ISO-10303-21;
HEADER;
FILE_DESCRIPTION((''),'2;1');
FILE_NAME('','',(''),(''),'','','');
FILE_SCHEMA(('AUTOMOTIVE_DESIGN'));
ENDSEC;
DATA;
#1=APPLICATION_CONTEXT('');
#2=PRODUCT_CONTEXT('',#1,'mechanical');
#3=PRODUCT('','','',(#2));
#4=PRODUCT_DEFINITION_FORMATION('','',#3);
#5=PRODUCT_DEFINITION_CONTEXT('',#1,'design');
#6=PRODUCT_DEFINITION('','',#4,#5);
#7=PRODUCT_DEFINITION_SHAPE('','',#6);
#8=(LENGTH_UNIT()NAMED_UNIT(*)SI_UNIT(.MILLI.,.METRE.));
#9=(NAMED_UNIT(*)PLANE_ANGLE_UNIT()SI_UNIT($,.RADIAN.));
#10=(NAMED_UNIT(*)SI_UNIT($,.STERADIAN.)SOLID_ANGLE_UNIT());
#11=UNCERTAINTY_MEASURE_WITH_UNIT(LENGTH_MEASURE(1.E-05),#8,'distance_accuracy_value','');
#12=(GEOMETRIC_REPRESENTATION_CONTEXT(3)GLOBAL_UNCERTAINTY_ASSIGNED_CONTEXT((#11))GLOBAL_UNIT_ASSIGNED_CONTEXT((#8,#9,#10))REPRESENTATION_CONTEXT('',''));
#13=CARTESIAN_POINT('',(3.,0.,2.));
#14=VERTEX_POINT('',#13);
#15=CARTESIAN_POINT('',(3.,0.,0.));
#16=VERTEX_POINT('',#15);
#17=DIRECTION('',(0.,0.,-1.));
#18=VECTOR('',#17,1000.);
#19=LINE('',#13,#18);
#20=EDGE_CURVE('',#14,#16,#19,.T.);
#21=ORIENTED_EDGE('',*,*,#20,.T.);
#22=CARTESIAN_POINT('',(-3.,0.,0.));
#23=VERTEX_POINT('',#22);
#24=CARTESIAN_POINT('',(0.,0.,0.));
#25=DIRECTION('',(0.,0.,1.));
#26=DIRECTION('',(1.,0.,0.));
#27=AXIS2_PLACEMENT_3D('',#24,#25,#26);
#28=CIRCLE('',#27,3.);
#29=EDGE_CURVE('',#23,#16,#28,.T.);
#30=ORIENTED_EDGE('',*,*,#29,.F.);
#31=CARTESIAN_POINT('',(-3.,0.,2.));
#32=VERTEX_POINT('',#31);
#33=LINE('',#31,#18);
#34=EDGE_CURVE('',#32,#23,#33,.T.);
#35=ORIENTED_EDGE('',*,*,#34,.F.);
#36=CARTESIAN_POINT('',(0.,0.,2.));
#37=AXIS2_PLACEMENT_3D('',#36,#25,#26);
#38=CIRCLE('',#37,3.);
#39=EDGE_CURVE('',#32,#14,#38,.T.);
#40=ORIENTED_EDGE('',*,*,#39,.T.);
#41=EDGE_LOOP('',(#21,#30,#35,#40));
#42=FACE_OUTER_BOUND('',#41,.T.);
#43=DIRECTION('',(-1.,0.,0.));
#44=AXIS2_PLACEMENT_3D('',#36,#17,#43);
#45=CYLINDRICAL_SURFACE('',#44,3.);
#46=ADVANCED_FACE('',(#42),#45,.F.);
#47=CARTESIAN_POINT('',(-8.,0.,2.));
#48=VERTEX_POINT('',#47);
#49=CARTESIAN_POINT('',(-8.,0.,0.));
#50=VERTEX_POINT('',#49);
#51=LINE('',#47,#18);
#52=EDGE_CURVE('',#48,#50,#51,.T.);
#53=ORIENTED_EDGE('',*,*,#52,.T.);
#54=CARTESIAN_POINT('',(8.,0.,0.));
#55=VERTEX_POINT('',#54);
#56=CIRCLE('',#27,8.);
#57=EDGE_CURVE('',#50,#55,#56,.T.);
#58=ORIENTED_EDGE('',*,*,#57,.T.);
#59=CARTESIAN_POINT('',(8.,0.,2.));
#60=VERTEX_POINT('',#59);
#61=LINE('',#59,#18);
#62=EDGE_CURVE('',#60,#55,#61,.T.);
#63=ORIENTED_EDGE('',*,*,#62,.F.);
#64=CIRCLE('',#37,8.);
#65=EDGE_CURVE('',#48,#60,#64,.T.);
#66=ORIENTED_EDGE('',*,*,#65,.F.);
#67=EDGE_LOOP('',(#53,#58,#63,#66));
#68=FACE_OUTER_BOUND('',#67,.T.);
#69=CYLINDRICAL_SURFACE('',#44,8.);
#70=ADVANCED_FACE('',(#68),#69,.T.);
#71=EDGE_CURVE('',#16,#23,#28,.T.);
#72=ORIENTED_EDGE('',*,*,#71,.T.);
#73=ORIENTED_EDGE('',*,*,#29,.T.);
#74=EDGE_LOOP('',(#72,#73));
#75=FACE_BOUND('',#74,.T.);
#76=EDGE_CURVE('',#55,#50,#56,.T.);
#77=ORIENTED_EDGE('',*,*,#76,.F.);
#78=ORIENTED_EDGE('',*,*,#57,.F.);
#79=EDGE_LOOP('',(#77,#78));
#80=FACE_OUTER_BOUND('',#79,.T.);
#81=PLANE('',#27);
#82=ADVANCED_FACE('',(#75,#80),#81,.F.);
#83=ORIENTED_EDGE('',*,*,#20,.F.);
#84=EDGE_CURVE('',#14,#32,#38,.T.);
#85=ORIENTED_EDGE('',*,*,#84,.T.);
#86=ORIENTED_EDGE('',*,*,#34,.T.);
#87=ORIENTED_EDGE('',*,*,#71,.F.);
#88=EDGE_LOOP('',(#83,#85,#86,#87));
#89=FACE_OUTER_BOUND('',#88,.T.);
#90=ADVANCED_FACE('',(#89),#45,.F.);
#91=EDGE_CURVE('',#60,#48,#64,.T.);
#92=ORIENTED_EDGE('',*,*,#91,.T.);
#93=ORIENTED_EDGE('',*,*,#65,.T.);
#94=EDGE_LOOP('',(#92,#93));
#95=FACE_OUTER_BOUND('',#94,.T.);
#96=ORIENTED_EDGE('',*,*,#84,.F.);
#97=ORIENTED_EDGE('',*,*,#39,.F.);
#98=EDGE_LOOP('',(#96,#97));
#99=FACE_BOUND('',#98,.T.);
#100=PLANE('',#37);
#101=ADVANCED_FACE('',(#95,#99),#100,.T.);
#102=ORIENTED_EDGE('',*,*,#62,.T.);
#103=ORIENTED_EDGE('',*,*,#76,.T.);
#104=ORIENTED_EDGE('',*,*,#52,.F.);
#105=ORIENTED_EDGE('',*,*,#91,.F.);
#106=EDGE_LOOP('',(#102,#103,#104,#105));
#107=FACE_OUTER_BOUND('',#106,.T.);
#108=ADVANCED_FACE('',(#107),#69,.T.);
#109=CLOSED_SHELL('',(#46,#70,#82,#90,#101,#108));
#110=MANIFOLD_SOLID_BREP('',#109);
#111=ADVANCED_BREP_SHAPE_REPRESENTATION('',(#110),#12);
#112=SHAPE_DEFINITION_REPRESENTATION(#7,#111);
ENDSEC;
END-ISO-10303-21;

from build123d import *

# Parameters (mm, degrees)
SKETCH_1_R      = 8
SKETCH_1_R_2    = 3
EXTRUDE_1_DEPTH = 2


with BuildPart() as part:
    # 草图1 → 凸台-拉伸1 (new body)
    with BuildSketch(Plane.XY):
        Circle(SKETCH_1_R)
        Circle(SKETCH_1_R_2, mode=Mode.SUBTRACT)
    extrude(amount=EXTRUDE_1_DEPTH)


solid = part.part
